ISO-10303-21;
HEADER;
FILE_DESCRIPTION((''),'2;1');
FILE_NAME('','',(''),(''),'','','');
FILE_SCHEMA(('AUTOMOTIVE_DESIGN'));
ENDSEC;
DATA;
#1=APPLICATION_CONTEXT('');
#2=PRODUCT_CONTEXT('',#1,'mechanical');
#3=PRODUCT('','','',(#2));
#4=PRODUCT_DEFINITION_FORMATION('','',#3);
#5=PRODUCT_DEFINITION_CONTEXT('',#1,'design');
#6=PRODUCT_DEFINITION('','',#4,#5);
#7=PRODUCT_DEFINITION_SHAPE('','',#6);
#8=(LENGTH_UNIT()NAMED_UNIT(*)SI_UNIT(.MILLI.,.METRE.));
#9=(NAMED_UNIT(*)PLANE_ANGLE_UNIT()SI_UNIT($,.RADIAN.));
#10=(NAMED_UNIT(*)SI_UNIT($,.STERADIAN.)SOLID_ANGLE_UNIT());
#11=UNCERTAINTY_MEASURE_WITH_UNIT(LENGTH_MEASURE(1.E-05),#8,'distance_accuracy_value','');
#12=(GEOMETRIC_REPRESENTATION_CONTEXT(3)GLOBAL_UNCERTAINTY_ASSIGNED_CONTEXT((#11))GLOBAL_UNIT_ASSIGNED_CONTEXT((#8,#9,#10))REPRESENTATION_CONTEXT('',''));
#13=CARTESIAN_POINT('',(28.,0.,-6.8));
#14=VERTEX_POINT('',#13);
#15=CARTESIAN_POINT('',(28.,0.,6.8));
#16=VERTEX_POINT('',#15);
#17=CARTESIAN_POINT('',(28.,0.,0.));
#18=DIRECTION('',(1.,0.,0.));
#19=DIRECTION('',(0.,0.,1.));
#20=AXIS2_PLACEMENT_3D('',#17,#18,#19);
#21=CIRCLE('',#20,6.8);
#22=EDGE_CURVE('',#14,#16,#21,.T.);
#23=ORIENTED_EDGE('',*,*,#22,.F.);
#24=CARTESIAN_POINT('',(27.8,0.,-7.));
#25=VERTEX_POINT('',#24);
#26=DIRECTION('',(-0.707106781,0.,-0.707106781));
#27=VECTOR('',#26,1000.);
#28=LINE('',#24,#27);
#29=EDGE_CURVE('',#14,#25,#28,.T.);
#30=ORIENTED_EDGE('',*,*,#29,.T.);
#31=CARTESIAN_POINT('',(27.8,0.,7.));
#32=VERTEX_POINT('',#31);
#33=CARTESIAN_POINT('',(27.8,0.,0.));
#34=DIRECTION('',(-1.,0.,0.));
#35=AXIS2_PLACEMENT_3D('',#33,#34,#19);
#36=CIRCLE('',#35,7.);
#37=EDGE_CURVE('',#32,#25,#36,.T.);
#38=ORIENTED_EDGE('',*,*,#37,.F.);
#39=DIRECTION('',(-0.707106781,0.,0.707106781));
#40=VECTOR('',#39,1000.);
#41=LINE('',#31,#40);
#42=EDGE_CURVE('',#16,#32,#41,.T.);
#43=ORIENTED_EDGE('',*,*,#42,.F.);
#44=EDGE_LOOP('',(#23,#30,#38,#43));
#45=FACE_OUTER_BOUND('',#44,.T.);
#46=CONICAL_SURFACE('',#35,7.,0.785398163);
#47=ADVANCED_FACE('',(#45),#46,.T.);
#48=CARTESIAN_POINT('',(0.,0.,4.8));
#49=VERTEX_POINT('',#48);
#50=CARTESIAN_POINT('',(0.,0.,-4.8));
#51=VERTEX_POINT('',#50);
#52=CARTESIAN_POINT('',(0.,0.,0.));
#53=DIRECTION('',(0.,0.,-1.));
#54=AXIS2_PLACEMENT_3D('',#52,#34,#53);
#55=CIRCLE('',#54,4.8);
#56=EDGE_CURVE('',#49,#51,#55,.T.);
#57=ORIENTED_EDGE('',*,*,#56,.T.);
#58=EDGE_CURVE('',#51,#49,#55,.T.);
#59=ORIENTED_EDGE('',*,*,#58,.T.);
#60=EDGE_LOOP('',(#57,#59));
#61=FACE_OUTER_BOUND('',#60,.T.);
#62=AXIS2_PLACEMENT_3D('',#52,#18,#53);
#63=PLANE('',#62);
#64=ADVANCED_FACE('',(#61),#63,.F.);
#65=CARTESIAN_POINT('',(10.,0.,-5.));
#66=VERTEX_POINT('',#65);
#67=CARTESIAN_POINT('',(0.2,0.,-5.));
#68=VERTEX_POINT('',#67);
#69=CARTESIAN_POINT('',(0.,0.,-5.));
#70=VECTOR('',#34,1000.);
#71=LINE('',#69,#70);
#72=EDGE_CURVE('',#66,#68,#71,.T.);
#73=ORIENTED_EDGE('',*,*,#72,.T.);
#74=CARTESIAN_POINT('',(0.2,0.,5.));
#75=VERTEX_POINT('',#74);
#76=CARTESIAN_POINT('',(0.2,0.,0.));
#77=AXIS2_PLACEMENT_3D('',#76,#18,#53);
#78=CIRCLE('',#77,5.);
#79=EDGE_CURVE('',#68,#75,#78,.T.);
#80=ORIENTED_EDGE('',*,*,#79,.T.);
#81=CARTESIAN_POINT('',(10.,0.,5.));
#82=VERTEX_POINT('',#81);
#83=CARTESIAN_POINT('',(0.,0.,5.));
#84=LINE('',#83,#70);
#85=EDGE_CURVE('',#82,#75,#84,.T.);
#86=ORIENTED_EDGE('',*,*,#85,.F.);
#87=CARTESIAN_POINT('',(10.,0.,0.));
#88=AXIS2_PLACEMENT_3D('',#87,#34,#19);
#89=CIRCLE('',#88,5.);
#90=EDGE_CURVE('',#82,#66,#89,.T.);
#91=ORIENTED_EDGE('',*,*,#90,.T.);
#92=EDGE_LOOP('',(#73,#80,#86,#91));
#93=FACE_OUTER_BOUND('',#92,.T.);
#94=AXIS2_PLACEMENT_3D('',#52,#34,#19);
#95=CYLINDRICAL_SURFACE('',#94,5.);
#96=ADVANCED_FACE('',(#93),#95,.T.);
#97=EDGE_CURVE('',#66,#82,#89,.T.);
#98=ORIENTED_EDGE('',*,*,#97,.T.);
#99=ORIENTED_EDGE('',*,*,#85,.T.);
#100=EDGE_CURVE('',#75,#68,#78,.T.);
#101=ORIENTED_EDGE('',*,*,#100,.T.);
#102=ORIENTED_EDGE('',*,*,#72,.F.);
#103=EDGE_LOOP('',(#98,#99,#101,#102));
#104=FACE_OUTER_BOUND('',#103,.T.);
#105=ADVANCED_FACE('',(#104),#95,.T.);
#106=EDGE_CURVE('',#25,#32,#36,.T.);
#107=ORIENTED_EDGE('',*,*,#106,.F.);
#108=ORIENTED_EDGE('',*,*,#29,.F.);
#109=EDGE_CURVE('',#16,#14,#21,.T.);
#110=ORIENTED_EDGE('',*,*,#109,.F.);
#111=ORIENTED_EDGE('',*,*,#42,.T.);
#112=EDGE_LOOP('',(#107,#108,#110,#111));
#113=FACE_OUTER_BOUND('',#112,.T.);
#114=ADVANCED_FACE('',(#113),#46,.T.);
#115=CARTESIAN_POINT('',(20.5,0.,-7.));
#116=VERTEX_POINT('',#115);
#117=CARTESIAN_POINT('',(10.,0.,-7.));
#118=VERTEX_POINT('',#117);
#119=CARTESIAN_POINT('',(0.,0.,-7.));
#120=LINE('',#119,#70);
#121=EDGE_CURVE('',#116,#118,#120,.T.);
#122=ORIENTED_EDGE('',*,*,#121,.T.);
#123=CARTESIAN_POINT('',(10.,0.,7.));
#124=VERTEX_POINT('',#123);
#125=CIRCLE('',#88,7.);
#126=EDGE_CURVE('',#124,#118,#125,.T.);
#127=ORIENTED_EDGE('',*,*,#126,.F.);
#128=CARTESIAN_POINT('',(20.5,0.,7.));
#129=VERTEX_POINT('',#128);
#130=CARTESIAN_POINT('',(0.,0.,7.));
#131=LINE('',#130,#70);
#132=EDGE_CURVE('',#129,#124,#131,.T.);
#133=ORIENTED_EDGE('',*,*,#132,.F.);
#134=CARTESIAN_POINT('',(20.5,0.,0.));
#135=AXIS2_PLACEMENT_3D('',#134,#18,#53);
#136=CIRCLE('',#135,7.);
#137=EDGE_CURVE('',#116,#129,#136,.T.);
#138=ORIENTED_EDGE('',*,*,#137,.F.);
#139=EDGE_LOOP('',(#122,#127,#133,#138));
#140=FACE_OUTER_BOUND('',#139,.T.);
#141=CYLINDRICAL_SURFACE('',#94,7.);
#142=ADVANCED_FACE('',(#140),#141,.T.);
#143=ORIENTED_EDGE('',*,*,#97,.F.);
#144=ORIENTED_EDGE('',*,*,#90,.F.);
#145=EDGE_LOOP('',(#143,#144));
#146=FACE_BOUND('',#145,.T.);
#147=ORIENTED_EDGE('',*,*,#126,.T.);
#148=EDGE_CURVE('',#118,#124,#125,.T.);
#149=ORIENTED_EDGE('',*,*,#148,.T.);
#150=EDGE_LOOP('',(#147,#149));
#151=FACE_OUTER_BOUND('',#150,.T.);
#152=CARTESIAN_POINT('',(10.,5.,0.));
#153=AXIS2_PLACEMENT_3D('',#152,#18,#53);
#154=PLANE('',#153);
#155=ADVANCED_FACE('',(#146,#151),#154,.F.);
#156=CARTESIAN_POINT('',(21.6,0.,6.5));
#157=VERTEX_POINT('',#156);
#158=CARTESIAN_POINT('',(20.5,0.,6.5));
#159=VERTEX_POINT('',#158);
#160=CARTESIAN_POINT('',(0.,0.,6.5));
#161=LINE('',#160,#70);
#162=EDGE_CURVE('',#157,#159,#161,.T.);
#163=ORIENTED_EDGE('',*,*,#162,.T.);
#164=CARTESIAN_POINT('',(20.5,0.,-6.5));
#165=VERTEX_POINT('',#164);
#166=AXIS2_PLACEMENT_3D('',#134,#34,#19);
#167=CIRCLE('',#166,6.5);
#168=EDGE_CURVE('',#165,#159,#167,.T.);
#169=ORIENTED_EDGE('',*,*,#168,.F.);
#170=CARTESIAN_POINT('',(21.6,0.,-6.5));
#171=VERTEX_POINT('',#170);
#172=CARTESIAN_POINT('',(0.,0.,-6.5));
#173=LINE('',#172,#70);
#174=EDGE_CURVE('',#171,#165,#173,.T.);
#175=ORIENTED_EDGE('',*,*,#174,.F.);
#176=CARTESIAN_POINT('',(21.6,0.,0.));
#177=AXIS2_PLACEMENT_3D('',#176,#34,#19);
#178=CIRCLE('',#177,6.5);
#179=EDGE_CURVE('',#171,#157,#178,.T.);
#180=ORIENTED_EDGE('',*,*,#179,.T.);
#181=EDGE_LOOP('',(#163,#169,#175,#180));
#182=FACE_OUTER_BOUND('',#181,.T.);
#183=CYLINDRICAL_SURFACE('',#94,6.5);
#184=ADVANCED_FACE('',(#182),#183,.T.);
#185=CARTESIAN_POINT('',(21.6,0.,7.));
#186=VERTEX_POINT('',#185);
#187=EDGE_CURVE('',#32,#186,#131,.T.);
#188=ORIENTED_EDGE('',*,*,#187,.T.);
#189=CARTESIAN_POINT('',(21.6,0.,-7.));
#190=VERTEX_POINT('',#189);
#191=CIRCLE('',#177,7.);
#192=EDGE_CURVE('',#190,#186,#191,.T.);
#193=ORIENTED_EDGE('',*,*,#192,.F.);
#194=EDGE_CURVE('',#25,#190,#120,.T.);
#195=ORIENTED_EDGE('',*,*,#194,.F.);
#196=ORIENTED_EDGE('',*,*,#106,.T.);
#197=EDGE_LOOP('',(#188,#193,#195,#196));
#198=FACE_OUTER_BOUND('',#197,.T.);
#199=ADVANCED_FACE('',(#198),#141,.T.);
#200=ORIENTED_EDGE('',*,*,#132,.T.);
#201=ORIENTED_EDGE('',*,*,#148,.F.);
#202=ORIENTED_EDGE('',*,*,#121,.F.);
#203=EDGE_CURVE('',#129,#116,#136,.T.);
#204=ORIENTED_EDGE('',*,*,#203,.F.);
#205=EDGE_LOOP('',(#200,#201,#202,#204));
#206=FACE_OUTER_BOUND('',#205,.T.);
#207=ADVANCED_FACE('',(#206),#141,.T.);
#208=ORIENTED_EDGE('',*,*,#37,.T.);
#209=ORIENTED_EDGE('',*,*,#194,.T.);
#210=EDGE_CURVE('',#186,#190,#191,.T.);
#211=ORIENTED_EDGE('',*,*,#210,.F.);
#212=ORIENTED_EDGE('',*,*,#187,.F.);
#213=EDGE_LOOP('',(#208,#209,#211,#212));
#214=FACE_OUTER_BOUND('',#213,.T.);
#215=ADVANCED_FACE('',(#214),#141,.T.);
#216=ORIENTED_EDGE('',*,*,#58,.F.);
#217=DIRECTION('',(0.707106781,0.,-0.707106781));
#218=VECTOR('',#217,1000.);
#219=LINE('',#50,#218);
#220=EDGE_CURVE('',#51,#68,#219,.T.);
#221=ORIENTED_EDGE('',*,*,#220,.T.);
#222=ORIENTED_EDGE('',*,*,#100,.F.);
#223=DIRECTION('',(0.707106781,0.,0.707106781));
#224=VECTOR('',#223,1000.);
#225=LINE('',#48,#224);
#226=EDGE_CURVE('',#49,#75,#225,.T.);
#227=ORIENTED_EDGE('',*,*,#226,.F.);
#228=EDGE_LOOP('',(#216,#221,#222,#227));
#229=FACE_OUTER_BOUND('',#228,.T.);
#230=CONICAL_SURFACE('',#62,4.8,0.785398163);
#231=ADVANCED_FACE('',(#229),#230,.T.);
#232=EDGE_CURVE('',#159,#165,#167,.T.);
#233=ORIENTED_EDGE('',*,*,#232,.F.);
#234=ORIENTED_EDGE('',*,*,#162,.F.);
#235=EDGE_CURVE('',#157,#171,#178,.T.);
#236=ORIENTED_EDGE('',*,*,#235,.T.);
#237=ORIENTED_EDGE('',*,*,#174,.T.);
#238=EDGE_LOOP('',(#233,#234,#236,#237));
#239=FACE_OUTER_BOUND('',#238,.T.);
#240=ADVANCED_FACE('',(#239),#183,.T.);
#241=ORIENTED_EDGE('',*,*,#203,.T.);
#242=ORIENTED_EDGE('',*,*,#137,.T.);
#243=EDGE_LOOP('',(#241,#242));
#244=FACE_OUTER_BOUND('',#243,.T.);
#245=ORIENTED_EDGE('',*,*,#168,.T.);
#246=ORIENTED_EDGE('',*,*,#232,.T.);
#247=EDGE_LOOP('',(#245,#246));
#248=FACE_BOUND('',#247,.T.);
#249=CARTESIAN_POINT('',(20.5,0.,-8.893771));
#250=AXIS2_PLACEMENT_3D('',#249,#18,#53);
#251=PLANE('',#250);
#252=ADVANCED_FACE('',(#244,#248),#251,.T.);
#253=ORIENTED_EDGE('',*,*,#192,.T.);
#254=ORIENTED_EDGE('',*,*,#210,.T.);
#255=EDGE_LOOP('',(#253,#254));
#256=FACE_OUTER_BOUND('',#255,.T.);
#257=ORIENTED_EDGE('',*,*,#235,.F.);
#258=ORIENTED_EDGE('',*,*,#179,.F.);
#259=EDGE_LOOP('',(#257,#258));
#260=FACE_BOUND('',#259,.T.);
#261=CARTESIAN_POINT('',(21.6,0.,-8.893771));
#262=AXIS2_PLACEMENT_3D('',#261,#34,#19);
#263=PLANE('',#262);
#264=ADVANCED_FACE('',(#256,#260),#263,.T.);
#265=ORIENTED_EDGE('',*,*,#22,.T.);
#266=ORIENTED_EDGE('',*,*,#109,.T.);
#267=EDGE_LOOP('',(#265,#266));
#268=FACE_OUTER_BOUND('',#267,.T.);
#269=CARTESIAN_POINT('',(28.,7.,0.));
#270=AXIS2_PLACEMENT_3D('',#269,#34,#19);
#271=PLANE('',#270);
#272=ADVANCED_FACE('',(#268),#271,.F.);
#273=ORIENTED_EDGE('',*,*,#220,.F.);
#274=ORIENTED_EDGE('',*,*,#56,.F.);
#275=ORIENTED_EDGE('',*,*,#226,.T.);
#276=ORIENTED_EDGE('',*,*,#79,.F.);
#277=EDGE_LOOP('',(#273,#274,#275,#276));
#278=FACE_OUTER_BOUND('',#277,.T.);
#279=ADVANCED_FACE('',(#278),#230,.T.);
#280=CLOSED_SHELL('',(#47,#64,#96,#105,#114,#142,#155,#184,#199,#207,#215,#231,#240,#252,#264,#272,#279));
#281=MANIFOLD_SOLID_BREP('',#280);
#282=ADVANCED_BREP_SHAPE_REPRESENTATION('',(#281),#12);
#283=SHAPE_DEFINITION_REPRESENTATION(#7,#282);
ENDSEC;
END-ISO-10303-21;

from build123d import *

# Parameters (mm, degrees)
CHAMFER1_SIZE = 0.2
CHAMFER2_SIZE = 0.2
SKETCH4_W     = 1.1
SKETCH4_H     = 2.393770958


with BuildPart() as part:
    # Sketch1 → Revolve1 (revolve)
    with BuildSketch(Plane.XY, mode=Mode.PRIVATE) as revolve1_sk:
        Polygon((0, 0), (0, 5), (10, 5), (10, 7), (28, 7), (28, 0), align=None)
    revolve(revolve1_sk.sketch.rotate(Axis((0, 0, 0), (1, 0, 0)), 90), axis=Axis((0, 0, 0), (1, 0, 0)))

    # Chamfer1
    chamfer1_edges = [part.edges().sort_by_distance(p)[0] for p in [
        (0, 0, -5),
    ]]
    chamfer(chamfer1_edges, length=CHAMFER1_SIZE)

    # Chamfer2
    chamfer2_edges = [part.edges().sort_by_distance(p)[0] for p in [
        (28, 0, -7),
    ]]
    chamfer(chamfer2_edges, length=CHAMFER2_SIZE)

    # Sketch4 → Cut-Revolve1 (revolve, cut)
    with BuildSketch(Plane(origin=(0, 0, 0), x_dir=(1, 0, 0), z_dir=(0, 1, 0)), mode=Mode.PRIVATE) as cut_revolve1_sk:
        with Locations((21.05, 7.696885479)):
            Rectangle(SKETCH4_W, SKETCH4_H)
    revolve(cut_revolve1_sk.sketch.rotate(Axis((0, 0, 0), (1, 0, 0)), 180), axis=Axis((0, 0, 0), (1, 0, 0)), mode=Mode.SUBTRACT)


solid = part.part
